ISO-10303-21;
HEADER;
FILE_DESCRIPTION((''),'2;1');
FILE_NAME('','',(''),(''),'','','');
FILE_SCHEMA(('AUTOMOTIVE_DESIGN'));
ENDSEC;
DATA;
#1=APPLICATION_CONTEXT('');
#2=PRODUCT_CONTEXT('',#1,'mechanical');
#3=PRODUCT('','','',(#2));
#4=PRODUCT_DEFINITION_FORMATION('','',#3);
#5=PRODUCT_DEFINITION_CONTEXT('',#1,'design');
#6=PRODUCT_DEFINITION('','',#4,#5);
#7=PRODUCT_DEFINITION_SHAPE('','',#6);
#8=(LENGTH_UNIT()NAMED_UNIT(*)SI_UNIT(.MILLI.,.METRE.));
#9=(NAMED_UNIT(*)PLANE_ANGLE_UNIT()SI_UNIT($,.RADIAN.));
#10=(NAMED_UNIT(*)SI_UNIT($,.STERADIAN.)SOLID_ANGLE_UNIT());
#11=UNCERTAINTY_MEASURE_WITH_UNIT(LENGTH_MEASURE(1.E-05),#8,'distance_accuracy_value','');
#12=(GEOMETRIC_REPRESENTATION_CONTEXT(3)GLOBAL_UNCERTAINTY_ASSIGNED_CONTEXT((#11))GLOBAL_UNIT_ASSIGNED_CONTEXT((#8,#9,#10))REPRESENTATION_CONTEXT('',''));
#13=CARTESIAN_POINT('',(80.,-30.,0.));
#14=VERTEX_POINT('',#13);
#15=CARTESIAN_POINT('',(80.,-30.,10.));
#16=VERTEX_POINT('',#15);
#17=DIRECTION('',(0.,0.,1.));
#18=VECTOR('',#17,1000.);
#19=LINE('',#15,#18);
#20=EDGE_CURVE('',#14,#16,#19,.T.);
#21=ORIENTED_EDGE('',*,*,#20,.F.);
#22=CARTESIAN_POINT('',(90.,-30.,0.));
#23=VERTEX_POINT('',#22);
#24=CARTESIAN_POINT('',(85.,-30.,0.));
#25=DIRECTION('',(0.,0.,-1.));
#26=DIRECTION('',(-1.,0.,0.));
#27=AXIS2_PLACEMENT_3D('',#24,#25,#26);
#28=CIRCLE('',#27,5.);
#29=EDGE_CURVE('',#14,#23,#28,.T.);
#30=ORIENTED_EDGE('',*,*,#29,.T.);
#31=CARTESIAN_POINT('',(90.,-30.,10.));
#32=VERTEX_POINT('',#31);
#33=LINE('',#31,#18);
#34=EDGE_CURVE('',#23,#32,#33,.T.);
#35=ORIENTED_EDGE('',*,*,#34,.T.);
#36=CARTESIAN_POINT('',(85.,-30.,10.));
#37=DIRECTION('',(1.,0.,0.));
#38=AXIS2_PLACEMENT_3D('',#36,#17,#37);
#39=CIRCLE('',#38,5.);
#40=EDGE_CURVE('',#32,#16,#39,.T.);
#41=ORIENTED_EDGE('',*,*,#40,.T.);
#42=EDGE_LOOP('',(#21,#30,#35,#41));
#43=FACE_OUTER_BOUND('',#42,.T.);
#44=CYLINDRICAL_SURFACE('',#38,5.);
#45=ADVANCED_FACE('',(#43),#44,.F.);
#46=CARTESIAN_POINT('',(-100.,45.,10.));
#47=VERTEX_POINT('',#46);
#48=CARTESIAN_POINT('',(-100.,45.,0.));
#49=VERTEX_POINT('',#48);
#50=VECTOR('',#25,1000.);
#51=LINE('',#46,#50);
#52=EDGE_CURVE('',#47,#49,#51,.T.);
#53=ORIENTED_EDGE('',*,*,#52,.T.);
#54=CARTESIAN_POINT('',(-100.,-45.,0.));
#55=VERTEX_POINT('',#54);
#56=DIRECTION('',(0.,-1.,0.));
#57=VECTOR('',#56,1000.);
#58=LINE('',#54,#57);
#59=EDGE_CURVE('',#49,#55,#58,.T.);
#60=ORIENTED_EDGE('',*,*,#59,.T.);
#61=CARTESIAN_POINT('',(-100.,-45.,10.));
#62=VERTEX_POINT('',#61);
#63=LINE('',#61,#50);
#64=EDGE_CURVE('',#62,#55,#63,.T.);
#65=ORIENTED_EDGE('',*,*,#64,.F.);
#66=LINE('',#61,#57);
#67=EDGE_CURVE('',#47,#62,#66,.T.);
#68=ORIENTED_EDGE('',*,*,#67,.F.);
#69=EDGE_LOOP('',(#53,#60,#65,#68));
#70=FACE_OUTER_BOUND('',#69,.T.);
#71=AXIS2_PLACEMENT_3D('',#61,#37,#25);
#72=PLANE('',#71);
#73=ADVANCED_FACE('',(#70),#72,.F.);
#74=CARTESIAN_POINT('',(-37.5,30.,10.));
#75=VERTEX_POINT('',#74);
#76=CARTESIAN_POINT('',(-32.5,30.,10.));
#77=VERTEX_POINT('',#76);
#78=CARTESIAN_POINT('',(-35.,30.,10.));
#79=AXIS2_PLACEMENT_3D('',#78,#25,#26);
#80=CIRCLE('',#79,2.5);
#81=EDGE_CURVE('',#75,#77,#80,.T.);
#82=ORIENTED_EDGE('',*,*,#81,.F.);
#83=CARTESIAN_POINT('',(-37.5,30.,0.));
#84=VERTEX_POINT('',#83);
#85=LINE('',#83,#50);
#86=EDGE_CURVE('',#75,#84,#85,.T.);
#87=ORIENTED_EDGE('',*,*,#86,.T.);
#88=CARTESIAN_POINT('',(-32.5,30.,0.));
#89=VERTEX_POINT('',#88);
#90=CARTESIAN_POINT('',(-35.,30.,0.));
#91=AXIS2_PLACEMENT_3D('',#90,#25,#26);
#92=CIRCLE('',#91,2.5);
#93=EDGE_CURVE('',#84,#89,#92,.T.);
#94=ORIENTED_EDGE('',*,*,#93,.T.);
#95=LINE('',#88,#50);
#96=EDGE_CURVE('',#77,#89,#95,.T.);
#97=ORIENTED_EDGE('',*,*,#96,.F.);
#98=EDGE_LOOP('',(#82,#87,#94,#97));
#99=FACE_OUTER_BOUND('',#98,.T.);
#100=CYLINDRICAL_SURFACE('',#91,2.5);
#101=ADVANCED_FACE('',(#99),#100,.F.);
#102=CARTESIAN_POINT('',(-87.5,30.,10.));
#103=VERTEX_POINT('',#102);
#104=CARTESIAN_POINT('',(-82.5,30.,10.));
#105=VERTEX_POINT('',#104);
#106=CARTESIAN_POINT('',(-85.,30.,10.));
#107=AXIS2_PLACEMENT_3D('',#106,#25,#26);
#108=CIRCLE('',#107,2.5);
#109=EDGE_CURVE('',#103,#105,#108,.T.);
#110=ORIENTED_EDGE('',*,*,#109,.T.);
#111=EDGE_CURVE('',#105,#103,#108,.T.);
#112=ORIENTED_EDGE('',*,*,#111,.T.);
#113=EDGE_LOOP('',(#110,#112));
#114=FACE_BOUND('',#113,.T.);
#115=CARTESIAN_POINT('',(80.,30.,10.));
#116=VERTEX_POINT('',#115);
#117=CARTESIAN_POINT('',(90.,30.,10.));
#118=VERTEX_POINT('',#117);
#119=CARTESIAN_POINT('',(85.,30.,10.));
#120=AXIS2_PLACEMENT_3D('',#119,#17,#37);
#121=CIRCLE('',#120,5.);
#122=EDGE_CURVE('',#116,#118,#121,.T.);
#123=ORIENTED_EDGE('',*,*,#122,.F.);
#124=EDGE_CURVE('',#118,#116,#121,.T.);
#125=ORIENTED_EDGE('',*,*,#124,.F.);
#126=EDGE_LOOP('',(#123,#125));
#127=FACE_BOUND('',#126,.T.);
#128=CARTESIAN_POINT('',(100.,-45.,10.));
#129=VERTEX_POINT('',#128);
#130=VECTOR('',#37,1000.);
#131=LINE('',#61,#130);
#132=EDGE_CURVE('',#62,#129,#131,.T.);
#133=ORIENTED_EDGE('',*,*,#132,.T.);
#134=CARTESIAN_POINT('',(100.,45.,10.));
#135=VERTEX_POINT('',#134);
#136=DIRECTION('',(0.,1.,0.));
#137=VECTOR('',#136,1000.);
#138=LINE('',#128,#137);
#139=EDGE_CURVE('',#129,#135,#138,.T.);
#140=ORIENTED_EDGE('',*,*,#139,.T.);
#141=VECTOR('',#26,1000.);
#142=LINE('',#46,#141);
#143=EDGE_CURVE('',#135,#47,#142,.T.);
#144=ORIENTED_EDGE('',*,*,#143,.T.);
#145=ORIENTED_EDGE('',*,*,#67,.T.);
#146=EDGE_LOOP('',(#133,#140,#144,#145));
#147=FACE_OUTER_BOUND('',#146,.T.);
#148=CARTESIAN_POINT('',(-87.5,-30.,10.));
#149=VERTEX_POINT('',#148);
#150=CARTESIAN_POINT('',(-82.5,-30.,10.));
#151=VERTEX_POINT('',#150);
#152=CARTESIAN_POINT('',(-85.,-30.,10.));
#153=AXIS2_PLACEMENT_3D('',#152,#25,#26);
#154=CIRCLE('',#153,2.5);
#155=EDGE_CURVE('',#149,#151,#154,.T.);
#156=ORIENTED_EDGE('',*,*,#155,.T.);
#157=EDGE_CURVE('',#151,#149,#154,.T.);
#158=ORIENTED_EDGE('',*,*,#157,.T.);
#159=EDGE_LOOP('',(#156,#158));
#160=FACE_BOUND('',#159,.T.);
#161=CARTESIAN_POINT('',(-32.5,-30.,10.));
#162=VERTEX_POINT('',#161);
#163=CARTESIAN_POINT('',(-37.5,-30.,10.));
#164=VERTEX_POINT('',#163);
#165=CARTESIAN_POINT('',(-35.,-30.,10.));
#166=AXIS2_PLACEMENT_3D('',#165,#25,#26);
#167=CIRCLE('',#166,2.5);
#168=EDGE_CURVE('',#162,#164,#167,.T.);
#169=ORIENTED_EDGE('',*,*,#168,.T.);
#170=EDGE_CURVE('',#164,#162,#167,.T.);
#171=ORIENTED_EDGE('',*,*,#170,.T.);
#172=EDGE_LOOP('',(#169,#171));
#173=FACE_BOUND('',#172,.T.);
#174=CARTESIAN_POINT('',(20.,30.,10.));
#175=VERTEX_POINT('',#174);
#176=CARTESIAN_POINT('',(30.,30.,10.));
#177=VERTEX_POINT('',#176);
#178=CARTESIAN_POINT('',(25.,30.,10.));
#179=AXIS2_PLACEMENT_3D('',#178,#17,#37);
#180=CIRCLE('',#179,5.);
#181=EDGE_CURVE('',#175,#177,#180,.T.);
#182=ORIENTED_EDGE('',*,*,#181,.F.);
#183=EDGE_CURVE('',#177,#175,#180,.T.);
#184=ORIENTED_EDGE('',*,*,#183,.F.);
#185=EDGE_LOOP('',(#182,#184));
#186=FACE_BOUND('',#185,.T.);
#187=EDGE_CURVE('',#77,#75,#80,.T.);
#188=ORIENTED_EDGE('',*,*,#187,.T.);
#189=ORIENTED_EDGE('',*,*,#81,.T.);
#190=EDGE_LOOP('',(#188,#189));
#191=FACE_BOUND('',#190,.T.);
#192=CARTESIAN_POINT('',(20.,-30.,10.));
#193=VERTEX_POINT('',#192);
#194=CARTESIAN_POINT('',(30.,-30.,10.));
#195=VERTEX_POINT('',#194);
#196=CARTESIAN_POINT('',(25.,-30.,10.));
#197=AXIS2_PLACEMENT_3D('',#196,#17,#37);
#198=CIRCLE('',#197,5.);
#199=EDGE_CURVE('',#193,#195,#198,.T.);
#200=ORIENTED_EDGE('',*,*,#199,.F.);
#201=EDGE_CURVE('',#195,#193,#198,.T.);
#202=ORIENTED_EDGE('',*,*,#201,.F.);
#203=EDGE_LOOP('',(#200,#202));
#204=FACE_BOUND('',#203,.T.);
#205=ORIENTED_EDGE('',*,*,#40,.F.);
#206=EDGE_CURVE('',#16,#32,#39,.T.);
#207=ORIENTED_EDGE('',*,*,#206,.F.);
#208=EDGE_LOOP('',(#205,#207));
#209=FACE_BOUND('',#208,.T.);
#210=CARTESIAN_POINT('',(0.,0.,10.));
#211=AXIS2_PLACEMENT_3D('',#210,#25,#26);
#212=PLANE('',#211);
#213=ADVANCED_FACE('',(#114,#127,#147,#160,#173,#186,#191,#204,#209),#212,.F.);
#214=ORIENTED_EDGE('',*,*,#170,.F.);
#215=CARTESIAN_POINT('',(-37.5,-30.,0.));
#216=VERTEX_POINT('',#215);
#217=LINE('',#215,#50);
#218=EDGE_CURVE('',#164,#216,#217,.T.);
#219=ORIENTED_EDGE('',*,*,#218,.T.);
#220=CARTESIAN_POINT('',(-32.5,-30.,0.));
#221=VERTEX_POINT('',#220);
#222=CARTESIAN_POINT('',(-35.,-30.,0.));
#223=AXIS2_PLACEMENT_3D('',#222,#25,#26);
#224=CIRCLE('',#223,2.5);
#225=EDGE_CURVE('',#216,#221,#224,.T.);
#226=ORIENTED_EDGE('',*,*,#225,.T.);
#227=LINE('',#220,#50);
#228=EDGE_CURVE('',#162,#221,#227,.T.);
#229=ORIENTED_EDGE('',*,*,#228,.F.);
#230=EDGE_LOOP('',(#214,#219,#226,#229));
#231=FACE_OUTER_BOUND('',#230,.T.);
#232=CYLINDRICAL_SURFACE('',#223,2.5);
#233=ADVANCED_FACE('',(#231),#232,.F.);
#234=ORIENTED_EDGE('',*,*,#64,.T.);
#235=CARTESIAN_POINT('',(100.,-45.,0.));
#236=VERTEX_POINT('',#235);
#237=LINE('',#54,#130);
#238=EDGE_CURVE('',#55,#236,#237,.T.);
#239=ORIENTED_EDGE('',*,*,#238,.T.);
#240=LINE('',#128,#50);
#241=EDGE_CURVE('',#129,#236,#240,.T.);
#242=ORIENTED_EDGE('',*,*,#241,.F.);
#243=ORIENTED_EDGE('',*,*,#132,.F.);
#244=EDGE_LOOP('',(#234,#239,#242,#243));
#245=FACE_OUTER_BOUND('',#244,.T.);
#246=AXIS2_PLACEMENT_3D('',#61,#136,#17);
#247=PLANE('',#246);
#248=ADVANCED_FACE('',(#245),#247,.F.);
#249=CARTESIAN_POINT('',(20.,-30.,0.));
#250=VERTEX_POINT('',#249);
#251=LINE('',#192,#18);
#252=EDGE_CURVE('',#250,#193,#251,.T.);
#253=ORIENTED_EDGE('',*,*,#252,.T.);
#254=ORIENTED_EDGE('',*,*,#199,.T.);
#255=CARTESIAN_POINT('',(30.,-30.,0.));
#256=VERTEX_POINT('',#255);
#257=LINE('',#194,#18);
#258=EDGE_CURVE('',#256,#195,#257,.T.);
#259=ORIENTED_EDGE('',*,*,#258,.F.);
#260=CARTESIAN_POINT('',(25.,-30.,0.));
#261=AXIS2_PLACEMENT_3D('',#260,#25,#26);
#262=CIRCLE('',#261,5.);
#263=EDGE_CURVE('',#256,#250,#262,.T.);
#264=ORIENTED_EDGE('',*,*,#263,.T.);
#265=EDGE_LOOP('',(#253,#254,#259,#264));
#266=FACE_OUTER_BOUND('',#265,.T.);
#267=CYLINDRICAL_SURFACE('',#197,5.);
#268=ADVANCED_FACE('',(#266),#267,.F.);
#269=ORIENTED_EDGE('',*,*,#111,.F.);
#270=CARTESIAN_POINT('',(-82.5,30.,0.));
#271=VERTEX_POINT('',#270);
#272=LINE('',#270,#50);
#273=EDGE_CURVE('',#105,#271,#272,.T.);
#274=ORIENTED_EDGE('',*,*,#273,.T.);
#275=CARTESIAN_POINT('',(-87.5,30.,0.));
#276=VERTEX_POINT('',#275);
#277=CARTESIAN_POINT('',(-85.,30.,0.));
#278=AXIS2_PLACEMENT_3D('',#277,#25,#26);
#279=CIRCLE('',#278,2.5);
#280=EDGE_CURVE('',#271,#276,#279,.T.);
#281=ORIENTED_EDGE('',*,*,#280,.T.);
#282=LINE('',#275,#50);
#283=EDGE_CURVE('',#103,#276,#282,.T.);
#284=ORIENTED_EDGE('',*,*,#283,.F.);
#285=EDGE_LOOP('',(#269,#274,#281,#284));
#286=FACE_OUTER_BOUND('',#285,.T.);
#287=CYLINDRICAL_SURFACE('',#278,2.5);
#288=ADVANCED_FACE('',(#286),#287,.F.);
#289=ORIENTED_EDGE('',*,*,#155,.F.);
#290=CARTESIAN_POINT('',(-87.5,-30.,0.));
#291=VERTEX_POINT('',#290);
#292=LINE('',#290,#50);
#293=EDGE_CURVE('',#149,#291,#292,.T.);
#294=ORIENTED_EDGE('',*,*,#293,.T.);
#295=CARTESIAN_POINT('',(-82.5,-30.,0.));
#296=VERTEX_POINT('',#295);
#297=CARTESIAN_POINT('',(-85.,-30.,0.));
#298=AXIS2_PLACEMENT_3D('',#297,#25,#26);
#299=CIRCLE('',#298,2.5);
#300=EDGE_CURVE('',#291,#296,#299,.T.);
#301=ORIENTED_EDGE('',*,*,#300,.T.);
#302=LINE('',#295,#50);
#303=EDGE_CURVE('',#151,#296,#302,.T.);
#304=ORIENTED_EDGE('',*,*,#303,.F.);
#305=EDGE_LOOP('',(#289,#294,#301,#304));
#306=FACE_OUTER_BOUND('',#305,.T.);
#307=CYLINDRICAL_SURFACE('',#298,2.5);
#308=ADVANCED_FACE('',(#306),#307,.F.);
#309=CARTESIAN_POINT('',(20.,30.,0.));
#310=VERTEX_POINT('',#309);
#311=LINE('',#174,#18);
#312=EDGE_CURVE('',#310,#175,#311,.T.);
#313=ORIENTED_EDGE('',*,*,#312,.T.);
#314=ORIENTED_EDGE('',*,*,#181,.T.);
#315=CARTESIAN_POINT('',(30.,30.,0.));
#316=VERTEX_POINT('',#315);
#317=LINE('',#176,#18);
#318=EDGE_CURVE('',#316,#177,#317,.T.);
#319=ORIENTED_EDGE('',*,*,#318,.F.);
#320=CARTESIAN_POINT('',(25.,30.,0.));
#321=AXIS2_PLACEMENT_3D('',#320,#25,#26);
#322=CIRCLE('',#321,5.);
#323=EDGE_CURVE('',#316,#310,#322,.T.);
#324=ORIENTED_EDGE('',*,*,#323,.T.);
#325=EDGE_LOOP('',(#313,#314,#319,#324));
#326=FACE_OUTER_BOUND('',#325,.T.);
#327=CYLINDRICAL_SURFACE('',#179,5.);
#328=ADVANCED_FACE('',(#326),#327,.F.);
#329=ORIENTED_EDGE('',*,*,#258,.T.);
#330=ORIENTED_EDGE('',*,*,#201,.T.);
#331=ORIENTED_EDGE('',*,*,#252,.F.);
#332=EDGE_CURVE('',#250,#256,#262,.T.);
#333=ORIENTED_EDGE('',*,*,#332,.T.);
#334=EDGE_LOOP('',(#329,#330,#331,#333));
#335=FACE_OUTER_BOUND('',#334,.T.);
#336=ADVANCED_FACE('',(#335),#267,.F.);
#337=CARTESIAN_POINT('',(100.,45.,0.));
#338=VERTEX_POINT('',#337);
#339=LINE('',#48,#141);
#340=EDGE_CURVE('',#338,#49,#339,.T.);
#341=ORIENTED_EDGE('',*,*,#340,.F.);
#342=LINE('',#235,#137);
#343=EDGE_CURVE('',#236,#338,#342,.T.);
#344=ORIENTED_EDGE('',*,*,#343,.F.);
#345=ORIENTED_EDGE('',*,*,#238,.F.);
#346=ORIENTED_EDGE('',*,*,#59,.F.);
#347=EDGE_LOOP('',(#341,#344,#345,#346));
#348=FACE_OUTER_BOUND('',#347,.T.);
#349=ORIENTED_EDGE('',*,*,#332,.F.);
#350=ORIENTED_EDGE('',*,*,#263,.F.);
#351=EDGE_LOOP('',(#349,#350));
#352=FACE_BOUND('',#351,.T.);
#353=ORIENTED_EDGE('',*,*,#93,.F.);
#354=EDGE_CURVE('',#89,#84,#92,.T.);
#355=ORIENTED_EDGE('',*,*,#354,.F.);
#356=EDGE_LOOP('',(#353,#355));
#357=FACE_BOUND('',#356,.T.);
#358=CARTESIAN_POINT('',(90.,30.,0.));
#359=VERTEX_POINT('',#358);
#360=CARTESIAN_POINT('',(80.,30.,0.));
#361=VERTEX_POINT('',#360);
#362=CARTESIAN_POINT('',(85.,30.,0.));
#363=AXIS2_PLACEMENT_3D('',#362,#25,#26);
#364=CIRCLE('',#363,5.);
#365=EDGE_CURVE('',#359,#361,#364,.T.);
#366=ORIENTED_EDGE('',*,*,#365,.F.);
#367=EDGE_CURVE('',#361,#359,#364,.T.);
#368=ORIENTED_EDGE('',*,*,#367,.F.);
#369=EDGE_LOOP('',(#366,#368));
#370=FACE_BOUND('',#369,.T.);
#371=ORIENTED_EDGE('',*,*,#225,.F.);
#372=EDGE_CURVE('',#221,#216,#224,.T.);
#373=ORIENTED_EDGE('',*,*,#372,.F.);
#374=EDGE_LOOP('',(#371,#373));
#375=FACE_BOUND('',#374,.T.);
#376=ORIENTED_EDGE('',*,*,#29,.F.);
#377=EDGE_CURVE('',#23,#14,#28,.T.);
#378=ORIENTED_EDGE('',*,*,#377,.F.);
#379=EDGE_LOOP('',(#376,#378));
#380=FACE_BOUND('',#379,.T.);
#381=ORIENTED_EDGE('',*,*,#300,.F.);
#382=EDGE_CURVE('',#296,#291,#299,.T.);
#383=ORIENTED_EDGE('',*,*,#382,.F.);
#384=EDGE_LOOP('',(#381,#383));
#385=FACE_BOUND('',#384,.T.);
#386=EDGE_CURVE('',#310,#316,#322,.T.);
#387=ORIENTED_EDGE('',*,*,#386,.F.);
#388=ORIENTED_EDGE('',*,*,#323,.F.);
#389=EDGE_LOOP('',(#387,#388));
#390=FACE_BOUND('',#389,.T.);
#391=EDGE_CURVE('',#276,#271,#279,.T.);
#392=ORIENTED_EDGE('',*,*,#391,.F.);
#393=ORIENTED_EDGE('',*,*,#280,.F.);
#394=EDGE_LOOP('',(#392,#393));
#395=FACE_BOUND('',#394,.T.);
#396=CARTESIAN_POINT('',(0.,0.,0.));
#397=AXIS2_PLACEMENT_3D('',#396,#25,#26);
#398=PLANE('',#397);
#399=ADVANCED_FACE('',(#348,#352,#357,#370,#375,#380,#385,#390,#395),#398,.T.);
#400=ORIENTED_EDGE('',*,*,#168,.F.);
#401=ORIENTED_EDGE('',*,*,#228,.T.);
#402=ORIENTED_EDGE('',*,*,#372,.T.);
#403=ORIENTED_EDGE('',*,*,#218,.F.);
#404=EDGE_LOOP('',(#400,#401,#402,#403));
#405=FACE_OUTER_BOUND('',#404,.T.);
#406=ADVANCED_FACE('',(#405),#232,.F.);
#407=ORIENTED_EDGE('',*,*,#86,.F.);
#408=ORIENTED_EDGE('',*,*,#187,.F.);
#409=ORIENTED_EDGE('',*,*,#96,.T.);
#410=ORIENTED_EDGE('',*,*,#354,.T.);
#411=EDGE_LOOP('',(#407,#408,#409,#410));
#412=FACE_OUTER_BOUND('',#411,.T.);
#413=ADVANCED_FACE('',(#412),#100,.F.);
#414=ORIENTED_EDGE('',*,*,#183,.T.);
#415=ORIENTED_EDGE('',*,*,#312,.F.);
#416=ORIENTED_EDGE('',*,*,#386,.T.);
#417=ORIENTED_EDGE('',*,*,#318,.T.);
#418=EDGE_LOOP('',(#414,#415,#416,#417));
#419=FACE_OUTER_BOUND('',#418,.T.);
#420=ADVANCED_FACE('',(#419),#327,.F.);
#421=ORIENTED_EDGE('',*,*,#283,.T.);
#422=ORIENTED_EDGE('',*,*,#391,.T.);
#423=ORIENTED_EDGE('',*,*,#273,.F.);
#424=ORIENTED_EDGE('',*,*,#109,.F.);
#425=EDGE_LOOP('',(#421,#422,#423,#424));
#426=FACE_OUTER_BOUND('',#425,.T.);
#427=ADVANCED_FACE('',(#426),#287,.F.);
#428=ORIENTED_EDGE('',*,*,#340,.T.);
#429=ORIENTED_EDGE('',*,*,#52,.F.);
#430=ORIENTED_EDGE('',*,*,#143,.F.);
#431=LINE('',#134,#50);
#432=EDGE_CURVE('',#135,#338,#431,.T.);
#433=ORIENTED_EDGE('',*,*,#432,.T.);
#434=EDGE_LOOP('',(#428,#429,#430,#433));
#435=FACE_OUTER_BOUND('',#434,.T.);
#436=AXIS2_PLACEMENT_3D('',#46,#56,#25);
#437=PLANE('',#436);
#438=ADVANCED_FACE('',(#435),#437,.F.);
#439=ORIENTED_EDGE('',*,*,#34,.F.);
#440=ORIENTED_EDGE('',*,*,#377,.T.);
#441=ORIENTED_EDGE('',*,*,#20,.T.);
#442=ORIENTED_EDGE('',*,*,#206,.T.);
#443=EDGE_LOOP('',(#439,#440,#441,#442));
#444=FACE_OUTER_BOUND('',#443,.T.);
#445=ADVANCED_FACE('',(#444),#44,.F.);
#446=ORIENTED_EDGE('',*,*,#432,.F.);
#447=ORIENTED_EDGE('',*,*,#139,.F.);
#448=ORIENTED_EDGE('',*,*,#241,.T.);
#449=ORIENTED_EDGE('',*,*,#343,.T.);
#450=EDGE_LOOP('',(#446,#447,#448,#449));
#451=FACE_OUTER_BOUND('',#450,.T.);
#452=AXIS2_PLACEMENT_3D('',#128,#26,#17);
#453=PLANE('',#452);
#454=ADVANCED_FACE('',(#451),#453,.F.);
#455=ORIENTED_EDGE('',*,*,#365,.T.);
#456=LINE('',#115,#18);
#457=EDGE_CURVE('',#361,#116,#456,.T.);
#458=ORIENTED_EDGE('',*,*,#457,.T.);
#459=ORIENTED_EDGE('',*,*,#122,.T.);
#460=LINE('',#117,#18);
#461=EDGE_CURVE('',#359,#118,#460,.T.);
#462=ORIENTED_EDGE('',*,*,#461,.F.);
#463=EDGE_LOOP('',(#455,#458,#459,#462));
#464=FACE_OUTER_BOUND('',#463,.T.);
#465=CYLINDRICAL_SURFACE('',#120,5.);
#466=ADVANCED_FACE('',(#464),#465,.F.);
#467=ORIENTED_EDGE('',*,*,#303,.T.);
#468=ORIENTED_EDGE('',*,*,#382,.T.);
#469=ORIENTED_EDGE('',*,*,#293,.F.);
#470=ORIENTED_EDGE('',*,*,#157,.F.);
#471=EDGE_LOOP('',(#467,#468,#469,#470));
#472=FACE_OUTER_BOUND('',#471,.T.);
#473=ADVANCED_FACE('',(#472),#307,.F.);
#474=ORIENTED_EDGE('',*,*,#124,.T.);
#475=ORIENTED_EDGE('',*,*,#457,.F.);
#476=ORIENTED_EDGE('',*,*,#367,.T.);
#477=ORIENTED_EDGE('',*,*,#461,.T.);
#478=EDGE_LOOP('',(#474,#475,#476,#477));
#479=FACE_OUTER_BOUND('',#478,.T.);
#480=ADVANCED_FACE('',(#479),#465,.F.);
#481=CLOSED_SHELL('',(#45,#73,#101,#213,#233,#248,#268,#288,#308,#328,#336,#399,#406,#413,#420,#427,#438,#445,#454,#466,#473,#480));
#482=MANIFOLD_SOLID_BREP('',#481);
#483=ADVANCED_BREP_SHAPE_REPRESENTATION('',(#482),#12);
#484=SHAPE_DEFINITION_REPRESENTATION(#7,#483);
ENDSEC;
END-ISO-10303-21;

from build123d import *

# Parameters (mm, degrees)
SKETCH_1_W             = 200
SKETCH_1_H             = 90
EXTRUDE_1_DEPTH        = 10
HOLE_WIZARD_M6_1_D     = 5
HOLE_WIZARD_M8_1_D     = 10
HOLE_WIZARD_M8_1_DEPTH = 30
HOLE_WIZARD_M8_1_TIP   = 3.004303095


with BuildPart() as part:
    # 草图1 → 凸台-拉伸1 (new body)
    with BuildSketch(Plane.XY):
        Rectangle(SKETCH_1_W, SKETCH_1_H)
    extrude(amount=EXTRUDE_1_DEPTH)

    # M6 螺纹孔1 (through all)
    with Locations(Plane(origin=(0, 0, 0), x_dir=(-1, 0, 0), z_dir=(0, 0, -1))):
        with Locations((85, 30), (35, -30), (85, -30), (35, 30)):
            Hole(HOLE_WIZARD_M6_1_D / 2)

    # M8 间隙孔1
    with Locations(Plane.XY.offset(10)):
        with Locations((85, -30), (85, 30), (25, -30), (25, 30)):
            Hole(HOLE_WIZARD_M8_1_D / 2, depth=HOLE_WIZARD_M8_1_DEPTH)
            with Locations((0, 0, -(HOLE_WIZARD_M8_1_DEPTH + HOLE_WIZARD_M8_1_TIP / 2))):  # 118° drill point
                Cone(0, HOLE_WIZARD_M8_1_D / 2, HOLE_WIZARD_M8_1_TIP, mode=Mode.SUBTRACT)


solid = part.part
